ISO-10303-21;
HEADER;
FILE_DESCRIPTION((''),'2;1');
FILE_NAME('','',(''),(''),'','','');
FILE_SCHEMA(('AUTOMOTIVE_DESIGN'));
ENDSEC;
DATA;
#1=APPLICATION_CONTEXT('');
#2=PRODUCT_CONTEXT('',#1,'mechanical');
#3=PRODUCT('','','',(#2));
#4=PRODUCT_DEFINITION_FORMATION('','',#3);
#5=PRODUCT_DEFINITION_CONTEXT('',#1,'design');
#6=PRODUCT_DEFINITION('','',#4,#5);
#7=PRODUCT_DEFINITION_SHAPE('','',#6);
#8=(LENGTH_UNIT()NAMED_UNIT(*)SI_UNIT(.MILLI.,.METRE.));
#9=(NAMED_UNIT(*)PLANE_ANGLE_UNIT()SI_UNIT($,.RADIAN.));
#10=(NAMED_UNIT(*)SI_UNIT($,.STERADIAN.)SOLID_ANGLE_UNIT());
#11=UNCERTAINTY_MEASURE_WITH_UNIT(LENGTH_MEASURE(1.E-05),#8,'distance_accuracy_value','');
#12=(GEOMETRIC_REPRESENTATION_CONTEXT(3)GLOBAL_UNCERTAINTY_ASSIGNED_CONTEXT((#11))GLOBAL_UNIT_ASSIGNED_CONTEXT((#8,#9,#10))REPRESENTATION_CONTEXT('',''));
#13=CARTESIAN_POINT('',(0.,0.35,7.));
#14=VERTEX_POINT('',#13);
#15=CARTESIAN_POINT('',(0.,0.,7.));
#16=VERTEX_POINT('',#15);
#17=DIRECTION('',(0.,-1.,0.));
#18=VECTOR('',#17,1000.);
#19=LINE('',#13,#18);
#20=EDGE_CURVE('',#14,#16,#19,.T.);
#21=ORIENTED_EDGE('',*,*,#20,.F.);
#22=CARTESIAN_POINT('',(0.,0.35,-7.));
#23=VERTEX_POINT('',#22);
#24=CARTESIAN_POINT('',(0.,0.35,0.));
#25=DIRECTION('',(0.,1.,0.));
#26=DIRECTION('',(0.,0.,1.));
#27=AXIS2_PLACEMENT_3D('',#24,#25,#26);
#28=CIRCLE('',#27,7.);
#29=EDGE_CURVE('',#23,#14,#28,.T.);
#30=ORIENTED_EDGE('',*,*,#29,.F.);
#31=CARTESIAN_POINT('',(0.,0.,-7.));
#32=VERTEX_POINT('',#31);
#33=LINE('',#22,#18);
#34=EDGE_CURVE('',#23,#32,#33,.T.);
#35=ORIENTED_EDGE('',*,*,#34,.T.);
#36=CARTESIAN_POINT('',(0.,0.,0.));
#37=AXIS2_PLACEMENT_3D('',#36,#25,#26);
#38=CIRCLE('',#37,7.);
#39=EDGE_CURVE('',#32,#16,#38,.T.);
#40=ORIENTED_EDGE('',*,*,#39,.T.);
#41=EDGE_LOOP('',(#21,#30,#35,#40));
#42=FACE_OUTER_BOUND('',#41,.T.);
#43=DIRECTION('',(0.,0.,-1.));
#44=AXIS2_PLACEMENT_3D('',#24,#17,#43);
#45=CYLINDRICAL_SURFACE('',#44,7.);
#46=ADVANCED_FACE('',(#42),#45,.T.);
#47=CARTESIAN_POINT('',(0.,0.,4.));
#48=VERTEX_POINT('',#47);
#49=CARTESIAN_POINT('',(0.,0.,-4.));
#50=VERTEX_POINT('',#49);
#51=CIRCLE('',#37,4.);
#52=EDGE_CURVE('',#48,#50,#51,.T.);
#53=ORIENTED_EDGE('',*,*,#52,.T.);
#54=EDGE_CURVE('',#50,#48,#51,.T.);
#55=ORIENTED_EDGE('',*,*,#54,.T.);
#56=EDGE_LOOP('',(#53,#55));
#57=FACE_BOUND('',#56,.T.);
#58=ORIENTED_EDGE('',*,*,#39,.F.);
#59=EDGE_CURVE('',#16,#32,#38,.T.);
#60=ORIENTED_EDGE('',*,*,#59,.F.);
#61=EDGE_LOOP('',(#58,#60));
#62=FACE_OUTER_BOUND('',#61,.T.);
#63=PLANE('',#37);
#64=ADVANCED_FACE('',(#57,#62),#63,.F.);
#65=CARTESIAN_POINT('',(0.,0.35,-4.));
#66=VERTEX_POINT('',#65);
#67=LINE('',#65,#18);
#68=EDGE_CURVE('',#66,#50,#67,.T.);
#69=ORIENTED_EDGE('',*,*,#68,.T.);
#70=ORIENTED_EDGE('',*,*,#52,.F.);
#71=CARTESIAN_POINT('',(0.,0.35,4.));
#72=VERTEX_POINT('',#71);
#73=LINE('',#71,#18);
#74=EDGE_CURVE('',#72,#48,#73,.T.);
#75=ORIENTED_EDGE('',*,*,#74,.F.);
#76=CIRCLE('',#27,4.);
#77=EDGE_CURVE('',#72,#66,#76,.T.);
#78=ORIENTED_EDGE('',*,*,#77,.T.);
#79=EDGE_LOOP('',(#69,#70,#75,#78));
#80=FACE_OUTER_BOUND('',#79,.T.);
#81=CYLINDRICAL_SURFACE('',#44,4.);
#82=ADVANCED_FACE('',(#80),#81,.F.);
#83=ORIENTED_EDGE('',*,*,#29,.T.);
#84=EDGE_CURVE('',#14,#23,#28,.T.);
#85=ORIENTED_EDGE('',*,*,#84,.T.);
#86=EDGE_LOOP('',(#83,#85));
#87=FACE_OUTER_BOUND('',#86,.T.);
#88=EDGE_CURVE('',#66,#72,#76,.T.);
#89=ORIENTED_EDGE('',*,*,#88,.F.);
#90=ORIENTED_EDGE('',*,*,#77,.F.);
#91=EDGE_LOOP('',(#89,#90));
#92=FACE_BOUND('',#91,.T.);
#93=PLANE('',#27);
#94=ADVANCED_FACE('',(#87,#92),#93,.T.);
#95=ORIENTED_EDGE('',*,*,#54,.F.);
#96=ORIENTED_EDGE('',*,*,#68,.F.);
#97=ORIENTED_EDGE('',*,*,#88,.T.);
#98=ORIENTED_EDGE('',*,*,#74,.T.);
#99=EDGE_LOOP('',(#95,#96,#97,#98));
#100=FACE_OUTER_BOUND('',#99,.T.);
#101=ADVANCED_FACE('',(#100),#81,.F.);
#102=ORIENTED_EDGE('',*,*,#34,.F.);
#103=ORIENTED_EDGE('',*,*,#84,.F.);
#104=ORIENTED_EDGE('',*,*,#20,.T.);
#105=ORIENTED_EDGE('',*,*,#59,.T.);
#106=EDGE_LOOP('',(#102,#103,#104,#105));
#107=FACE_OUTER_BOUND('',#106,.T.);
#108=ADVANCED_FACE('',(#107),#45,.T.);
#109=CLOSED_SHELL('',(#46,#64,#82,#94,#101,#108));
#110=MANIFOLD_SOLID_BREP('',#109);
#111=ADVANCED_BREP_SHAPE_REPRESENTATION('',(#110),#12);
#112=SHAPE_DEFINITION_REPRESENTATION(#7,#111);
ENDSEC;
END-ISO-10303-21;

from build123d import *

# Parameters (mm, degrees)
SKETCH1_R           = 7
SKETCH1_R_2         = 4
BOSS_EXTRUDE1_DEPTH = 0.35


with BuildPart() as part:
    # Sketch1 → Boss-Extrude1 (new body)
    with BuildSketch(Plane(origin=(0, 0, 0), x_dir=(1, 0, 0), z_dir=(0, 1, 0))):
        with Locations(Location((0, 0, 0), (0, 0, 270))):
            Circle(SKETCH1_R)
        with Locations(Location((0, 0, 0), (0, 0, 270))):
            Circle(SKETCH1_R_2, mode=Mode.SUBTRACT)
    extrude(amount=BOSS_EXTRUDE1_DEPTH)


solid = part.part
